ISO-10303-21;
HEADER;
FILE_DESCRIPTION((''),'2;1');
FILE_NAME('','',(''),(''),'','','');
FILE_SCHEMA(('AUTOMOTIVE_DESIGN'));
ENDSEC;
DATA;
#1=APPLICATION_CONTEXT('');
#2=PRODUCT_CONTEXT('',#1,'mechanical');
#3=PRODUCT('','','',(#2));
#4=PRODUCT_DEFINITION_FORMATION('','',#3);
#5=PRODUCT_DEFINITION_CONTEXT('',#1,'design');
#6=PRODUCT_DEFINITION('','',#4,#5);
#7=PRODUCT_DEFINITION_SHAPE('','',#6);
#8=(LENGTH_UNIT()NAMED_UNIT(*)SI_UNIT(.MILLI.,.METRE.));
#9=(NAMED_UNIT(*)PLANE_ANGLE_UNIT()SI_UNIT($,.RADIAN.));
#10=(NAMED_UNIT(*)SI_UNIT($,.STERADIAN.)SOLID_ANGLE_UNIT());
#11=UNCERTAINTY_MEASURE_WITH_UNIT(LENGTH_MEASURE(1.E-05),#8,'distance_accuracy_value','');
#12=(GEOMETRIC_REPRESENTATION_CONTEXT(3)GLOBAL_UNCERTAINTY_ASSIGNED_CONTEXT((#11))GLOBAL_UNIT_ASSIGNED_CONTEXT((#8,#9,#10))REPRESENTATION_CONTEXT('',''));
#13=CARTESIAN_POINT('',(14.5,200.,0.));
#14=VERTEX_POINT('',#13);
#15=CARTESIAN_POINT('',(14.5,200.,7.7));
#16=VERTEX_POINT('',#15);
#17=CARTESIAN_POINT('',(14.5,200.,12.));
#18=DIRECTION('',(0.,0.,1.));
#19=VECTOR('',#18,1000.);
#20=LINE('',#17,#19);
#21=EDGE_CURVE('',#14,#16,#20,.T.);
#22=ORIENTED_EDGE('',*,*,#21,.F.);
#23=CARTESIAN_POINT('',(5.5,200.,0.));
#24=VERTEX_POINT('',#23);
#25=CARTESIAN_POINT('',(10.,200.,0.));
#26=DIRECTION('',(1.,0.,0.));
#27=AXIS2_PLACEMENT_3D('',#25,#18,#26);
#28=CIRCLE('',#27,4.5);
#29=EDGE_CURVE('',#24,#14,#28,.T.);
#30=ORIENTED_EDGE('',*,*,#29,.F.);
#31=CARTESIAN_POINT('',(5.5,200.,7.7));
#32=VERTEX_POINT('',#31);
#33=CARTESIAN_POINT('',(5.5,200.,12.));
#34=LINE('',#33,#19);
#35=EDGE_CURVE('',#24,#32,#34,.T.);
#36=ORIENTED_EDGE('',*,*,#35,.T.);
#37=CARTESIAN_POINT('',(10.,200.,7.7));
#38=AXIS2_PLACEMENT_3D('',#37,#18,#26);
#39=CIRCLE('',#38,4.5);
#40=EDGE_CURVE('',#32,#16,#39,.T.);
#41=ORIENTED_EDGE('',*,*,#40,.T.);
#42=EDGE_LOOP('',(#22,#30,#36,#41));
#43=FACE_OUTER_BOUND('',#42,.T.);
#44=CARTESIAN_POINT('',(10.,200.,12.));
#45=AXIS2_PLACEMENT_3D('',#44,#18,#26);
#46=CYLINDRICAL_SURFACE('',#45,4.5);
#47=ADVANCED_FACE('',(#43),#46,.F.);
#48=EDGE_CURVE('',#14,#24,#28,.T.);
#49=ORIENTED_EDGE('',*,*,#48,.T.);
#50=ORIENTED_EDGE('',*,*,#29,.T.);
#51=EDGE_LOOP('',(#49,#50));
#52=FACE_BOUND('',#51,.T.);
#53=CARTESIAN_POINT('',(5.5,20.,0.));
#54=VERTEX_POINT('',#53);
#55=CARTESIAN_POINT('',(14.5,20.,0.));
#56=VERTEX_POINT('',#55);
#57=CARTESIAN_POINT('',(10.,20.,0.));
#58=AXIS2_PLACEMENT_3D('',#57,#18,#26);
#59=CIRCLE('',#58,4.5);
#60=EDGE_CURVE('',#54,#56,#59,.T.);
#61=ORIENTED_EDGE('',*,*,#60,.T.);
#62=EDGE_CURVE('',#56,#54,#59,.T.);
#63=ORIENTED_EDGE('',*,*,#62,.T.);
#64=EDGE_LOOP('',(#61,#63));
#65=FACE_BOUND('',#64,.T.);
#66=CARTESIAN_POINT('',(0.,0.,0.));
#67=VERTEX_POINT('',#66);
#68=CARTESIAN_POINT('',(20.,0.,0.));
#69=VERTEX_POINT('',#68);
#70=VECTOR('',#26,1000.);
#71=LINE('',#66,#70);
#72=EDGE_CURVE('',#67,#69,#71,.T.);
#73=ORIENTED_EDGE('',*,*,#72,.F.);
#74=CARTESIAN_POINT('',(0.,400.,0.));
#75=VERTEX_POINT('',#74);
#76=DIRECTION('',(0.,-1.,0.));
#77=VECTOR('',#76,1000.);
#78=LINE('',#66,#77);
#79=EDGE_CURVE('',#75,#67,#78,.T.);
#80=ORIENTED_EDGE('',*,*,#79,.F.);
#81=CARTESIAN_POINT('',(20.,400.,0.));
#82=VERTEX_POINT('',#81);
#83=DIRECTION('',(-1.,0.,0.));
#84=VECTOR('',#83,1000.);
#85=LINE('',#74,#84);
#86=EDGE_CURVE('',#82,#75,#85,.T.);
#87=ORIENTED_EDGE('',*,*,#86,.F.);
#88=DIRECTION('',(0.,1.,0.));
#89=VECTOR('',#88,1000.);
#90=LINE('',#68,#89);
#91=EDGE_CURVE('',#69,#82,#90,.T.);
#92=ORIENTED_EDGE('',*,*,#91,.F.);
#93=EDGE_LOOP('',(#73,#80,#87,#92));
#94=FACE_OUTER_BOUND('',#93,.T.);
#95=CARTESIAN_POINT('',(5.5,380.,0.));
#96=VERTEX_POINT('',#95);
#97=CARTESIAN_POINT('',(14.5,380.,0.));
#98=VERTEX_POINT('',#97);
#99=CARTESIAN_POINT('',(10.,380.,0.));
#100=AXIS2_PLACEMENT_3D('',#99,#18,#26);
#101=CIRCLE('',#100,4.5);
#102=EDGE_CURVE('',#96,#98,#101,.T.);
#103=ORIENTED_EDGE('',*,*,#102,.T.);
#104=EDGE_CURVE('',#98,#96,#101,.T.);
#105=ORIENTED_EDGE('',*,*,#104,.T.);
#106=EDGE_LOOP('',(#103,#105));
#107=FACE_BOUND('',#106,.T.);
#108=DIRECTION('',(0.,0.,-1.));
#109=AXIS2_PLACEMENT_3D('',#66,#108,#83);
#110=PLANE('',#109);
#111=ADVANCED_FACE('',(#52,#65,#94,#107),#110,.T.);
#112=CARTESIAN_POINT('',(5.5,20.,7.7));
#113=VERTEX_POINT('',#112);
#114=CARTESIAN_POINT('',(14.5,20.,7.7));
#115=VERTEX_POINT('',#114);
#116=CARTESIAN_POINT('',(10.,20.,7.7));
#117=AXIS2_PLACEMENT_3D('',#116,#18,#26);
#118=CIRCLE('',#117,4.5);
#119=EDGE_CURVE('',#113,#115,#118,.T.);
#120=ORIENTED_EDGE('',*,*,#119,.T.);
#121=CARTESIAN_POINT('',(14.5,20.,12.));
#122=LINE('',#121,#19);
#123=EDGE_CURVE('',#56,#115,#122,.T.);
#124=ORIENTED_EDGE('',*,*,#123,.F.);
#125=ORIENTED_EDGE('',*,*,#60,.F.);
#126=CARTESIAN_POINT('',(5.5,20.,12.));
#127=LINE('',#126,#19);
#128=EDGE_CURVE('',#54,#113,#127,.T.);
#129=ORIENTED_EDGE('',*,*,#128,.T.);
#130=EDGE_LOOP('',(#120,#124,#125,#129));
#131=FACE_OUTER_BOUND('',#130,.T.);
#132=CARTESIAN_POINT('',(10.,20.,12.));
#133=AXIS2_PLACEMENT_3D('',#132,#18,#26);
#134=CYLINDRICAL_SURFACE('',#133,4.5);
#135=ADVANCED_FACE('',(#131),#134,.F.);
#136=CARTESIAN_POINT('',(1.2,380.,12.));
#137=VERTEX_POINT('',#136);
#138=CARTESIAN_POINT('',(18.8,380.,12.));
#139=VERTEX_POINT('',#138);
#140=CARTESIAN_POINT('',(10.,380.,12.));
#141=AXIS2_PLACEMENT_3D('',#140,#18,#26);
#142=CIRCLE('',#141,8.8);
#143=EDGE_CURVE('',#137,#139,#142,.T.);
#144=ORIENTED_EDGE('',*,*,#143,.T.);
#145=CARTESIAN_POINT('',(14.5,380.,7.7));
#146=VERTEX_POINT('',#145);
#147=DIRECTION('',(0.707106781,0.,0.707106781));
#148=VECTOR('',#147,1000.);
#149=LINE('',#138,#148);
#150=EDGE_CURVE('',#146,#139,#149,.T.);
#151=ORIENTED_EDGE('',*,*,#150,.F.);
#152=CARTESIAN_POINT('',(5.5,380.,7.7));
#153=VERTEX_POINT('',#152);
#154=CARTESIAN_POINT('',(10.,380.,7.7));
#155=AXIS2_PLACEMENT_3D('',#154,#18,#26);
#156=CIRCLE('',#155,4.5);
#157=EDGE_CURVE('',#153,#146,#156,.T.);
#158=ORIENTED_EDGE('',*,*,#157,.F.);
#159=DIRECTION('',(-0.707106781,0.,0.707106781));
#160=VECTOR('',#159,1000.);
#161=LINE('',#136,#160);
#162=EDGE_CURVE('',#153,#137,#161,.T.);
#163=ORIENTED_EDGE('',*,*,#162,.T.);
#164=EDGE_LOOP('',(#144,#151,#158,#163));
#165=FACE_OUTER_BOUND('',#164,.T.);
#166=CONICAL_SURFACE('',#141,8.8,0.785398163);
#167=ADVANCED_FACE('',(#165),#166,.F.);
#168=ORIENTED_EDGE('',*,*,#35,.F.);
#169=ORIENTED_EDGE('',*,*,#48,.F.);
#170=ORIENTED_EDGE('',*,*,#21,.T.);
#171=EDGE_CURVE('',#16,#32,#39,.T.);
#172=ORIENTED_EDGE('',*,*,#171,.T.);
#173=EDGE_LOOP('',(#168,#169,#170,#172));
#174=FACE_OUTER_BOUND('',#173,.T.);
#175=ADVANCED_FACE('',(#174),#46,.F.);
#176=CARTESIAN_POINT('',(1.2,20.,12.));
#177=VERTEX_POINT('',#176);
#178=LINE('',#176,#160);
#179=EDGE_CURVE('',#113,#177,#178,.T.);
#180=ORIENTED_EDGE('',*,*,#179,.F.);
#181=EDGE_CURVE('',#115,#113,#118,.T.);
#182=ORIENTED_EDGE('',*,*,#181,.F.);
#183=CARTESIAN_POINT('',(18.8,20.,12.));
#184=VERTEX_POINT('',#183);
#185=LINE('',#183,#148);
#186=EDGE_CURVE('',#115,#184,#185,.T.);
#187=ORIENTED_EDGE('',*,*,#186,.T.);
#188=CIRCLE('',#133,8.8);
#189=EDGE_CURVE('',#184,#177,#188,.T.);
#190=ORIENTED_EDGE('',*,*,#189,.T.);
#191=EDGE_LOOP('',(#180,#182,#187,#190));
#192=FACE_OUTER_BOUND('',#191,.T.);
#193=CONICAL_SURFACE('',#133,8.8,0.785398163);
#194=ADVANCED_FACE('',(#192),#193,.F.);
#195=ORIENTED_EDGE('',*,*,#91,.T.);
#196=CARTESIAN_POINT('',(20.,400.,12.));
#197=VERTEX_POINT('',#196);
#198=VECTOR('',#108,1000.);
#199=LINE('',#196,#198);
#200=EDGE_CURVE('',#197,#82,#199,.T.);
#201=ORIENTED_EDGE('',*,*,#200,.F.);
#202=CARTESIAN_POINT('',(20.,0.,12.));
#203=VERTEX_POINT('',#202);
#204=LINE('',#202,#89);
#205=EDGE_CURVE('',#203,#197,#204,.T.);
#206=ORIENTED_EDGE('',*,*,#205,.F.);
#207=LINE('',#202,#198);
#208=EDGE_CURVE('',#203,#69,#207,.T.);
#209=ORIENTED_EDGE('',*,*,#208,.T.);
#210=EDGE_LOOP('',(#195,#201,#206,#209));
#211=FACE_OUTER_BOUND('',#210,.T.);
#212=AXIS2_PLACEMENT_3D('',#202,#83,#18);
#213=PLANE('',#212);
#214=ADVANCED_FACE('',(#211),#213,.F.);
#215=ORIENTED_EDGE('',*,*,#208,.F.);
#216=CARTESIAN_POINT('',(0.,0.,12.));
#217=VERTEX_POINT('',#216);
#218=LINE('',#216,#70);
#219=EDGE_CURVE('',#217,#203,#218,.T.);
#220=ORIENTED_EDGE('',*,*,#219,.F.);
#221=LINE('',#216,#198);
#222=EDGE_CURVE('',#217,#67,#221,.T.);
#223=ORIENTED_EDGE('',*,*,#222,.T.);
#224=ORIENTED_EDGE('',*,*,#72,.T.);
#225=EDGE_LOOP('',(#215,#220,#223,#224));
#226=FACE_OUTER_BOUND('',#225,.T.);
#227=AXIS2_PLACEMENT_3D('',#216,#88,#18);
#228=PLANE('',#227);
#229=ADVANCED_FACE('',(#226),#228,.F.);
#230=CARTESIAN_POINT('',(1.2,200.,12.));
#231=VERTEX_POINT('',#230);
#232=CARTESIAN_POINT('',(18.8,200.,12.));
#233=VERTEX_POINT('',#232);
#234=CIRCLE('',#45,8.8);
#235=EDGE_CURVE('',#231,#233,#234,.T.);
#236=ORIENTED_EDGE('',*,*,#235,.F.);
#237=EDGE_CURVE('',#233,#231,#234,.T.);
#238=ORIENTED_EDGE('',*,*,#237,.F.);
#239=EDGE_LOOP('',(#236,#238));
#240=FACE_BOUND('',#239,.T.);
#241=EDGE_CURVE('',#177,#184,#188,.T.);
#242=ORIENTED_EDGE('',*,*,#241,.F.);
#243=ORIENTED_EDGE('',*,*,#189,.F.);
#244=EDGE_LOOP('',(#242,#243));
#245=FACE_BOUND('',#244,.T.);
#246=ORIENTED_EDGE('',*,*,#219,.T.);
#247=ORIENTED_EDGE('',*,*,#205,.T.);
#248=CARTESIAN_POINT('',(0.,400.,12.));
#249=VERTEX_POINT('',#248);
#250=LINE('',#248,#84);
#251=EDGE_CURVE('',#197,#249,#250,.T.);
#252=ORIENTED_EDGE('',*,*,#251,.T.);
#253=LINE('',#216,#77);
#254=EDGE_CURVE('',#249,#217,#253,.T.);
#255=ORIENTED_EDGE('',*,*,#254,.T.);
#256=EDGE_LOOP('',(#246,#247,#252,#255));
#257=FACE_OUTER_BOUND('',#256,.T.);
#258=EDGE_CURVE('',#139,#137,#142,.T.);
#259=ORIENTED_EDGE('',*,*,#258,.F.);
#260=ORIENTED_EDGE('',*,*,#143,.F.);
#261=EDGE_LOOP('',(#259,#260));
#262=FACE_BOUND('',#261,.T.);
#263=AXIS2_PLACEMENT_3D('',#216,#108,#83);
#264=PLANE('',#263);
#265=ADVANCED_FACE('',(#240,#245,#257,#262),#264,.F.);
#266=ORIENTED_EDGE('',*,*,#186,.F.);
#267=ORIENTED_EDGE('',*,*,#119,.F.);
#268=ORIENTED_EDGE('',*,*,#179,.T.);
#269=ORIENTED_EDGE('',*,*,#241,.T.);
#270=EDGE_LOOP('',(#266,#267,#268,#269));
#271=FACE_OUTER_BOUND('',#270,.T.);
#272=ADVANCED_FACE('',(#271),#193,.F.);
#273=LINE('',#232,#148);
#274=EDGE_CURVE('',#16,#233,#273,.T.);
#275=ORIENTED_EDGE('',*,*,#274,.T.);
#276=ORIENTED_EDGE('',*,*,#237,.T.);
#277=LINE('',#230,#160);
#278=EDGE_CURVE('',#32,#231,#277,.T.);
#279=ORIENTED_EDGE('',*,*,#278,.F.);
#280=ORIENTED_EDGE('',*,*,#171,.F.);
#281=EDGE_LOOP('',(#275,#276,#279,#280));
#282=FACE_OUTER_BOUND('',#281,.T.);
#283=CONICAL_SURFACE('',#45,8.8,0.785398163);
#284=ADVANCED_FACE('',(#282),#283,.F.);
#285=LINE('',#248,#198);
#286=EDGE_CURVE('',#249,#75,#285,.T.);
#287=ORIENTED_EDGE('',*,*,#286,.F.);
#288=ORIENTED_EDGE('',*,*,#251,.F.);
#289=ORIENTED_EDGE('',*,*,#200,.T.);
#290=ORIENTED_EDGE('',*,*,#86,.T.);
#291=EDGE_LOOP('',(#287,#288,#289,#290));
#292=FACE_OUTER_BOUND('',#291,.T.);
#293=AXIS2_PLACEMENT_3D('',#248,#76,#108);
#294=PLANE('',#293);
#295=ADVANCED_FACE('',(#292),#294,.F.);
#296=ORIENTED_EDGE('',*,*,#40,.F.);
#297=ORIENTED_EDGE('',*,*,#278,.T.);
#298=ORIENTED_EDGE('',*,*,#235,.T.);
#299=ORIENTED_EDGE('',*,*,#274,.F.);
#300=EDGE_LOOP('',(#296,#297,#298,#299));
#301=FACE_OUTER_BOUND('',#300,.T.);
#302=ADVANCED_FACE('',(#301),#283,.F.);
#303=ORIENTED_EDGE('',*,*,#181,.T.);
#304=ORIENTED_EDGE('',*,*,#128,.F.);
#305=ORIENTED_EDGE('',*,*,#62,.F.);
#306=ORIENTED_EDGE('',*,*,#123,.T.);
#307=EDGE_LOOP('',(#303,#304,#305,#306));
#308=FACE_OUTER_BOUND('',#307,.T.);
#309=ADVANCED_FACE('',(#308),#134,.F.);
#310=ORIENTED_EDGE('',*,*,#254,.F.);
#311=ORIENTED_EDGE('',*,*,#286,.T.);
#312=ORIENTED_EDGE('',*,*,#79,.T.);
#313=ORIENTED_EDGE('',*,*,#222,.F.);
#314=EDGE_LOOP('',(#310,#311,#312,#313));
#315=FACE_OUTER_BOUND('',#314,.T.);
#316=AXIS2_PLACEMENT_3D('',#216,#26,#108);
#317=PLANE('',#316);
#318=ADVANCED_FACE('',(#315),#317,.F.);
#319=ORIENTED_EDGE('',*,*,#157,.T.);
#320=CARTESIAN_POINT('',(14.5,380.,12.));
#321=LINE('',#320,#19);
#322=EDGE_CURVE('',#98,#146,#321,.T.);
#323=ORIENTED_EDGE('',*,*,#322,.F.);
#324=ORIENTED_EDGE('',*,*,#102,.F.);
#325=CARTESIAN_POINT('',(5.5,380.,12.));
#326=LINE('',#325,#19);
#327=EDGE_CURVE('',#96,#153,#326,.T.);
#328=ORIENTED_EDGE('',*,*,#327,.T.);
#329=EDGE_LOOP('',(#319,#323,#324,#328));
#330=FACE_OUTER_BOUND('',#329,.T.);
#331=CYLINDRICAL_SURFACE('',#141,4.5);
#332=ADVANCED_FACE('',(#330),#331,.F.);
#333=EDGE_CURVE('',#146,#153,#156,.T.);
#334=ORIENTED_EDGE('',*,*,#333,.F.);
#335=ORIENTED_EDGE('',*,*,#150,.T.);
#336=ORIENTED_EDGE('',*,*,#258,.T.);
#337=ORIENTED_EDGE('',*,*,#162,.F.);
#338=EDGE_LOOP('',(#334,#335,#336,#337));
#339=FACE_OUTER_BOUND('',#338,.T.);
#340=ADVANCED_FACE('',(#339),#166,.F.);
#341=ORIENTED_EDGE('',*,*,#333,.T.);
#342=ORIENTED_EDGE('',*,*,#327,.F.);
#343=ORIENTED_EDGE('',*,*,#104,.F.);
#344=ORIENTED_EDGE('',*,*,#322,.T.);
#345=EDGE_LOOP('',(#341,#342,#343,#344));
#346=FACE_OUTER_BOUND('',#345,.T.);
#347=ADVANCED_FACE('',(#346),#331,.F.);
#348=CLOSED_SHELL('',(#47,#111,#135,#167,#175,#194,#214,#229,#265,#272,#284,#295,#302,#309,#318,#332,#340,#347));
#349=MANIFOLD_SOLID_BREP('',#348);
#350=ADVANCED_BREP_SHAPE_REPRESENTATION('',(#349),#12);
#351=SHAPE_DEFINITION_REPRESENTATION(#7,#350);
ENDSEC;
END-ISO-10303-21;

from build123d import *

# Parameters (mm, degrees)
SKETCH1_W                                           = 20
SKETCH1_H                                           = 400
BOSS_EXTRUDE1_DEPTH                                 = 12
HOLE_SIZE_BY_HEX_SOCKET_FLAT_COUNTERSUN_D           = 9
HOLE_SIZE_BY_HEX_SOCKET_FLAT_COUNTERSUN_CSINK_D     = 17.6
HOLE_SIZE_BY_HEX_SOCKET_FLAT_COUNTERSUN_CSINK_ANGLE = 90


with BuildPart() as part:
    # Sketch1 → Boss-Extrude1 (new body)
    with BuildSketch(Plane.XY):
        with Locations((10, 200)):
            Rectangle(SKETCH1_W, SKETCH1_H)
    extrude(amount=BOSS_EXTRUDE1_DEPTH)

    # Hole size (by hex socket flat countersunk head screw type)1 (through all)
    with Locations(Plane.XY.offset(12)):
        with Locations((10, 380), (10, 200), (10, 20)):
            CounterSinkHole(HOLE_SIZE_BY_HEX_SOCKET_FLAT_COUNTERSUN_D / 2, HOLE_SIZE_BY_HEX_SOCKET_FLAT_COUNTERSUN_CSINK_D / 2, counter_sink_angle=HOLE_SIZE_BY_HEX_SOCKET_FLAT_COUNTERSUN_CSINK_ANGLE)


solid = part.part
